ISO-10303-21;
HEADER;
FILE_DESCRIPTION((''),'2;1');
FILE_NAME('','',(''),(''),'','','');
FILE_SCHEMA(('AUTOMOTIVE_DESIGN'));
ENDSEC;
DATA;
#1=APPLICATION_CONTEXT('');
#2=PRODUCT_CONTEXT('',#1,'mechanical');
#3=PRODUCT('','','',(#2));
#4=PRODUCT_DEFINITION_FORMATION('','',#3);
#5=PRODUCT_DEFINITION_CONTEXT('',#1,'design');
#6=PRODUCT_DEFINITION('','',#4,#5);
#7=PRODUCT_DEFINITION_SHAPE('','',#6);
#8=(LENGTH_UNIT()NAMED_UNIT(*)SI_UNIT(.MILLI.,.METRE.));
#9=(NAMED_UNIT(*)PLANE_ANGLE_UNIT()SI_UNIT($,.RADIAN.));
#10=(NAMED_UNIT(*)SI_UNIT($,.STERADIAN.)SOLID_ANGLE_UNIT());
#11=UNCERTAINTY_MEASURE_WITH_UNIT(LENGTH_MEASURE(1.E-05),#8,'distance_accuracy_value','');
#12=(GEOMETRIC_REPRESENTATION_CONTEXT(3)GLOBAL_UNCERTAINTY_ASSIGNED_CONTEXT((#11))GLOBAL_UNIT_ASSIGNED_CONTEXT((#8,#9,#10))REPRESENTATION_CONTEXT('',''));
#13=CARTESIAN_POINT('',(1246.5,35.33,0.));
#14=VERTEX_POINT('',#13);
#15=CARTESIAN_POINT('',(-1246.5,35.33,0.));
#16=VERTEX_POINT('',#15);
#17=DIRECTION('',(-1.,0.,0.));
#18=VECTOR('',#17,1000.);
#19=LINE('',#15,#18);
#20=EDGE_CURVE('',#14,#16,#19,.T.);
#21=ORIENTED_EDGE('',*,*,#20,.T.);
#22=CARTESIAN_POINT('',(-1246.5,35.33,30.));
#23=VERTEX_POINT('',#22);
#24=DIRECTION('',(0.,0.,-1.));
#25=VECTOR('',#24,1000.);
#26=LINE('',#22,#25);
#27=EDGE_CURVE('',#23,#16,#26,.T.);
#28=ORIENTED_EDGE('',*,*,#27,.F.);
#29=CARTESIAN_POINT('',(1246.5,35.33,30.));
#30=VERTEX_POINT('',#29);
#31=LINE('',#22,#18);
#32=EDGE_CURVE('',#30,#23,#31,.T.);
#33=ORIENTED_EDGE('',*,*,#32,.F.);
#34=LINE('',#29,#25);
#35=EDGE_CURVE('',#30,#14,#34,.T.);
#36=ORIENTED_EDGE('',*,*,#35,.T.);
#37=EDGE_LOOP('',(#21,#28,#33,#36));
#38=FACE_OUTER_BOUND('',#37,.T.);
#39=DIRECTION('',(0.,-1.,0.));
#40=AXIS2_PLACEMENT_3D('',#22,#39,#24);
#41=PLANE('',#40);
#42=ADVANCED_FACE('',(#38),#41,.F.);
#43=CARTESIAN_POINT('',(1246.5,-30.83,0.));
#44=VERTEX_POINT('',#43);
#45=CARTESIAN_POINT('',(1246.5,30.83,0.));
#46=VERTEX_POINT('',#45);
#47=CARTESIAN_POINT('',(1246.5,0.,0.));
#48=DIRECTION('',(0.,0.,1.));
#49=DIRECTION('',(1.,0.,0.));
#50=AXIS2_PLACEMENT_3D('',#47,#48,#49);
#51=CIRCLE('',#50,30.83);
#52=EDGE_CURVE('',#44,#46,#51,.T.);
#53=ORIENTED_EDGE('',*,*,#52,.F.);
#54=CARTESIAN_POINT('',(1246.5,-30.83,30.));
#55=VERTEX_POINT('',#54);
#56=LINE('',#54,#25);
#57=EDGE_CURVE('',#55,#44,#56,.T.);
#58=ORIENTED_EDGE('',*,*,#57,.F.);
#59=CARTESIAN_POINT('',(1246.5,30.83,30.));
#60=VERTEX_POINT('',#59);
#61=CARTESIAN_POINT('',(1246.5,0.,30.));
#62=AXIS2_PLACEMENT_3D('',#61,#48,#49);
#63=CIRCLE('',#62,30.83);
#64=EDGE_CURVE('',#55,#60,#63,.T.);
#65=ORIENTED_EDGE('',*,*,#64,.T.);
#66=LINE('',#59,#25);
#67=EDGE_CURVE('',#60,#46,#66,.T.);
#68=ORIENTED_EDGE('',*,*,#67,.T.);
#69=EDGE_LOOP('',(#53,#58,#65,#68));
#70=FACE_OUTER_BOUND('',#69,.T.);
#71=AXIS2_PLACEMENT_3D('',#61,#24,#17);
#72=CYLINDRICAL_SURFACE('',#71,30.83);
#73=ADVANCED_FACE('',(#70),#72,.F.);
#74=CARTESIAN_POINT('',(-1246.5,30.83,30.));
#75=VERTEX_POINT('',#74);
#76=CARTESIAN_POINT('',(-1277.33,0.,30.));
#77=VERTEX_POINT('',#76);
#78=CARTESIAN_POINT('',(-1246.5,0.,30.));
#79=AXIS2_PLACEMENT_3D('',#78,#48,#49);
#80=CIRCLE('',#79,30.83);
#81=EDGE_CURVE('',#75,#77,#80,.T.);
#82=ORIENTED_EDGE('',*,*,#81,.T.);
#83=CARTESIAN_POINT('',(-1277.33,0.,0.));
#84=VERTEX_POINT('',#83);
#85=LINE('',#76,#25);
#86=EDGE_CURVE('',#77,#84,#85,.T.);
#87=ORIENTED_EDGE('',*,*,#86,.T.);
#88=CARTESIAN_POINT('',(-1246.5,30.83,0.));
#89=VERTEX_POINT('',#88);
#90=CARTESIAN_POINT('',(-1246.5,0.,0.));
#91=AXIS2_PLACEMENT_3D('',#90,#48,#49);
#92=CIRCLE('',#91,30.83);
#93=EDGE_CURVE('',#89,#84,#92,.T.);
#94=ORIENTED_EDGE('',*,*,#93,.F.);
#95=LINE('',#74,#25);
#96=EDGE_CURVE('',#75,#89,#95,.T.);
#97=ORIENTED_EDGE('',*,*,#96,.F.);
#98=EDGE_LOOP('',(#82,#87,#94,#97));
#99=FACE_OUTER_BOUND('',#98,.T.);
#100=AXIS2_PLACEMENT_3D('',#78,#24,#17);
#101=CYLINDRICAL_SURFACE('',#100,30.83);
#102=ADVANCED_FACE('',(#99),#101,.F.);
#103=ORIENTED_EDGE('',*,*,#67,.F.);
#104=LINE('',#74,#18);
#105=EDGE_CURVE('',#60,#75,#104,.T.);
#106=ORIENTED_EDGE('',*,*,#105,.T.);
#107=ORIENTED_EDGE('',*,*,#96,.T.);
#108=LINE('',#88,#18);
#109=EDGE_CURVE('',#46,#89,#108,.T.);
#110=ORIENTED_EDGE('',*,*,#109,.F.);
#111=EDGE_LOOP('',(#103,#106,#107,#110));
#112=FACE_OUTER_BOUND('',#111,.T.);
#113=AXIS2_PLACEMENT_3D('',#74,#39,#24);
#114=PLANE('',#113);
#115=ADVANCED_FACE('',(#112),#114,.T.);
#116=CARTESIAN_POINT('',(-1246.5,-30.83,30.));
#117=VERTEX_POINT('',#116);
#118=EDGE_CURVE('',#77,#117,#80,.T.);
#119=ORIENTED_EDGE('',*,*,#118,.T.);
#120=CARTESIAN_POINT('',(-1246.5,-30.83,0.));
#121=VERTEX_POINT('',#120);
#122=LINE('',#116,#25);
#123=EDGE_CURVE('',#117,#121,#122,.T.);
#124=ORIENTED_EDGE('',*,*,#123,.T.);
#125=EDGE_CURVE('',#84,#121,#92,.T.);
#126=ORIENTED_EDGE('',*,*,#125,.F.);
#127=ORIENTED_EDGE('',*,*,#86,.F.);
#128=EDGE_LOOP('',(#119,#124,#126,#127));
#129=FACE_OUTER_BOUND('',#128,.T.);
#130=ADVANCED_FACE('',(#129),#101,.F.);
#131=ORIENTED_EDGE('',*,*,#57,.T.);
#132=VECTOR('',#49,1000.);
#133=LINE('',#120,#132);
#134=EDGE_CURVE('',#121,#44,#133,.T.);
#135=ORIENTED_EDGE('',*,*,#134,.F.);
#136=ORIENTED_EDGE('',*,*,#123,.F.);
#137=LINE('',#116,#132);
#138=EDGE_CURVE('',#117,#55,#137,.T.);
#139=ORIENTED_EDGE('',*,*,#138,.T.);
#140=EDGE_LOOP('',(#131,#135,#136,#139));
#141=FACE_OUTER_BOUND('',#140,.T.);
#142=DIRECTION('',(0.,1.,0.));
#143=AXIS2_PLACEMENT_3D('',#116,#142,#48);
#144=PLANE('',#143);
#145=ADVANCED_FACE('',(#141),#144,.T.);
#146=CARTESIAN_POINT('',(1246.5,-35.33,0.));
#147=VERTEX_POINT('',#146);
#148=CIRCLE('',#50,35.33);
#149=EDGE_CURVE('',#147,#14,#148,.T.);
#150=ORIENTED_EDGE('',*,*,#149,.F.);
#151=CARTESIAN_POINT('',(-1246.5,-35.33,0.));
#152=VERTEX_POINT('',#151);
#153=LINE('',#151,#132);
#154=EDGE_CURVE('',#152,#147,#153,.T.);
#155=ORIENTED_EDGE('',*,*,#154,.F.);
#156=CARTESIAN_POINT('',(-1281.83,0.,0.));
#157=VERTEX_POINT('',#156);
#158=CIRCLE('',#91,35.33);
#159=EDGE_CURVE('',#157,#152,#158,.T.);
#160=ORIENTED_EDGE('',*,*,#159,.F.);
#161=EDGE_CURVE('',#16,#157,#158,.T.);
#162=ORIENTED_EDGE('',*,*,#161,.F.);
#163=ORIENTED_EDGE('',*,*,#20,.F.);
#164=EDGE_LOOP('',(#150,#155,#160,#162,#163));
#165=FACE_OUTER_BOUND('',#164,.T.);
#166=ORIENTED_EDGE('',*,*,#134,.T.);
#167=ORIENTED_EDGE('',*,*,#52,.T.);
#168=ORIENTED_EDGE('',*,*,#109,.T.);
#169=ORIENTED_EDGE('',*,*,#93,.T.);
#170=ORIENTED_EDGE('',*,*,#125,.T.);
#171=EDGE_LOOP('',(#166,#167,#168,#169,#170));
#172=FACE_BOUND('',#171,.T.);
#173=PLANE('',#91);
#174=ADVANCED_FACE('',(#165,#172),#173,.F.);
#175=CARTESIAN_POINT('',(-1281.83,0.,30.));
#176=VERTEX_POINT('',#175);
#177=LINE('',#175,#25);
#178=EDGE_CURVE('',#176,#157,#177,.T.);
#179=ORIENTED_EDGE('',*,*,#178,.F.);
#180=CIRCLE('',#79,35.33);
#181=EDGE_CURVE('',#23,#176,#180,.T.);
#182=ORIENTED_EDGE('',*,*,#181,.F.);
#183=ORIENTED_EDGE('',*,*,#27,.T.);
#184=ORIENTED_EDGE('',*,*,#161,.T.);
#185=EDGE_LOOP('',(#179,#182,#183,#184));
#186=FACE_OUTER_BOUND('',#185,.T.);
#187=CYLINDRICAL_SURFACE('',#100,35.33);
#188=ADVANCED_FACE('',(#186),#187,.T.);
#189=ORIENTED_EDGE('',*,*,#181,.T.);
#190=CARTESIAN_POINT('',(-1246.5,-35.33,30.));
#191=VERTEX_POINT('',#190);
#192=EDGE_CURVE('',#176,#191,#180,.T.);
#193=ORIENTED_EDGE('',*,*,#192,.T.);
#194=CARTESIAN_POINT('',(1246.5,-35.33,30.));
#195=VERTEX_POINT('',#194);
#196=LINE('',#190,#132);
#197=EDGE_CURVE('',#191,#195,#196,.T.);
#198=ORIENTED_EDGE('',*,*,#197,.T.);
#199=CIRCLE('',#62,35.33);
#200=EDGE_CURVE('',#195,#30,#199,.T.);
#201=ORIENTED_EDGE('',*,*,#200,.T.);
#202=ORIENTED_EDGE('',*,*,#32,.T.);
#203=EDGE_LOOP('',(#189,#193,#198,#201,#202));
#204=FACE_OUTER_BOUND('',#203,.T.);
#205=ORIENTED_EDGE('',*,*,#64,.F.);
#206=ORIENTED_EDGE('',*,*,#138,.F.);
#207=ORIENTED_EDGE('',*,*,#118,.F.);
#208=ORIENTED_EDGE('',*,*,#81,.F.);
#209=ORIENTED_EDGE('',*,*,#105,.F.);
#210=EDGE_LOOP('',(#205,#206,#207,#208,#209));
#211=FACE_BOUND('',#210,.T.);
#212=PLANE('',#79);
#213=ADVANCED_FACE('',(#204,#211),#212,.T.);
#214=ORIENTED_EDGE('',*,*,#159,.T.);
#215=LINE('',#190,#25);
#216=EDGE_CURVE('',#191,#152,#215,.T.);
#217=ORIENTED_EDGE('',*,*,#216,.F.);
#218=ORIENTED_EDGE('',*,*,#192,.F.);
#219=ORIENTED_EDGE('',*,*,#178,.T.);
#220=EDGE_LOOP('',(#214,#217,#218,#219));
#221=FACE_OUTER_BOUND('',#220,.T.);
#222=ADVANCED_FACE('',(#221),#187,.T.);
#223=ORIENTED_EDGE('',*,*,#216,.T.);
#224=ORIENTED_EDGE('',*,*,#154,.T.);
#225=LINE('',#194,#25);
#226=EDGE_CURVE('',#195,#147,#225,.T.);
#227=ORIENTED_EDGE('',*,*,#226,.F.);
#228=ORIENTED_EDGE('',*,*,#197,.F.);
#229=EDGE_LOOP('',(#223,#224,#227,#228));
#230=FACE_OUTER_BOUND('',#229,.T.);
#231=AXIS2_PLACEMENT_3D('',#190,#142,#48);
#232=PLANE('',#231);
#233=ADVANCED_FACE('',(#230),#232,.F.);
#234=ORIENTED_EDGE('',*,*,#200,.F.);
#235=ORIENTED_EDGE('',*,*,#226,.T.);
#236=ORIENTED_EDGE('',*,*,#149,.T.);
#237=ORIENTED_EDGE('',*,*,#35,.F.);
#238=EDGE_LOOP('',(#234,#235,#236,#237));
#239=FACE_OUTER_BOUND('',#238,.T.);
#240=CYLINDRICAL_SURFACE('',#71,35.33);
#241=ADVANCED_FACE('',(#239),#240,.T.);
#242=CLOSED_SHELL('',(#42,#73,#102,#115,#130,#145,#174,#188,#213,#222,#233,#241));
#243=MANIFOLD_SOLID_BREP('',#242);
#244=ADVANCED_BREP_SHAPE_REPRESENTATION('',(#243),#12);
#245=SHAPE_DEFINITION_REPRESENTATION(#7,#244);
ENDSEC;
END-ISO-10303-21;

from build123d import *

# Parameters (mm, degrees)
EXTRUDE_1_DEPTH = 30


with BuildPart() as part:
    # 草图1 → 拉伸-薄壁1 (new body)
    with BuildSketch(Plane.XY):
        with BuildLine():
            Line((1246.5, -35.33), (-1246.5, -35.33))
            ThreePointArc((-1246.5, -35.33), (-1281.83, 0), (-1246.5, 35.33))
            Line((-1246.5, 35.33), (1246.5, 35.33))
            ThreePointArc((1246.5, 35.33), (1281.83, 0), (1246.5, -35.33))
        make_face()
        with BuildLine():
            Line((1246.5, -30.83), (-1246.5, -30.83))
            ThreePointArc((-1246.5, -30.83), (-1277.33, 0), (-1246.5, 30.83))
            Line((-1246.5, 30.83), (1246.5, 30.83))
            ThreePointArc((1246.5, 30.83), (1277.33, 0), (1246.5, -30.83))
        make_face(mode=Mode.SUBTRACT)
    extrude(amount=EXTRUDE_1_DEPTH)


solid = part.part
